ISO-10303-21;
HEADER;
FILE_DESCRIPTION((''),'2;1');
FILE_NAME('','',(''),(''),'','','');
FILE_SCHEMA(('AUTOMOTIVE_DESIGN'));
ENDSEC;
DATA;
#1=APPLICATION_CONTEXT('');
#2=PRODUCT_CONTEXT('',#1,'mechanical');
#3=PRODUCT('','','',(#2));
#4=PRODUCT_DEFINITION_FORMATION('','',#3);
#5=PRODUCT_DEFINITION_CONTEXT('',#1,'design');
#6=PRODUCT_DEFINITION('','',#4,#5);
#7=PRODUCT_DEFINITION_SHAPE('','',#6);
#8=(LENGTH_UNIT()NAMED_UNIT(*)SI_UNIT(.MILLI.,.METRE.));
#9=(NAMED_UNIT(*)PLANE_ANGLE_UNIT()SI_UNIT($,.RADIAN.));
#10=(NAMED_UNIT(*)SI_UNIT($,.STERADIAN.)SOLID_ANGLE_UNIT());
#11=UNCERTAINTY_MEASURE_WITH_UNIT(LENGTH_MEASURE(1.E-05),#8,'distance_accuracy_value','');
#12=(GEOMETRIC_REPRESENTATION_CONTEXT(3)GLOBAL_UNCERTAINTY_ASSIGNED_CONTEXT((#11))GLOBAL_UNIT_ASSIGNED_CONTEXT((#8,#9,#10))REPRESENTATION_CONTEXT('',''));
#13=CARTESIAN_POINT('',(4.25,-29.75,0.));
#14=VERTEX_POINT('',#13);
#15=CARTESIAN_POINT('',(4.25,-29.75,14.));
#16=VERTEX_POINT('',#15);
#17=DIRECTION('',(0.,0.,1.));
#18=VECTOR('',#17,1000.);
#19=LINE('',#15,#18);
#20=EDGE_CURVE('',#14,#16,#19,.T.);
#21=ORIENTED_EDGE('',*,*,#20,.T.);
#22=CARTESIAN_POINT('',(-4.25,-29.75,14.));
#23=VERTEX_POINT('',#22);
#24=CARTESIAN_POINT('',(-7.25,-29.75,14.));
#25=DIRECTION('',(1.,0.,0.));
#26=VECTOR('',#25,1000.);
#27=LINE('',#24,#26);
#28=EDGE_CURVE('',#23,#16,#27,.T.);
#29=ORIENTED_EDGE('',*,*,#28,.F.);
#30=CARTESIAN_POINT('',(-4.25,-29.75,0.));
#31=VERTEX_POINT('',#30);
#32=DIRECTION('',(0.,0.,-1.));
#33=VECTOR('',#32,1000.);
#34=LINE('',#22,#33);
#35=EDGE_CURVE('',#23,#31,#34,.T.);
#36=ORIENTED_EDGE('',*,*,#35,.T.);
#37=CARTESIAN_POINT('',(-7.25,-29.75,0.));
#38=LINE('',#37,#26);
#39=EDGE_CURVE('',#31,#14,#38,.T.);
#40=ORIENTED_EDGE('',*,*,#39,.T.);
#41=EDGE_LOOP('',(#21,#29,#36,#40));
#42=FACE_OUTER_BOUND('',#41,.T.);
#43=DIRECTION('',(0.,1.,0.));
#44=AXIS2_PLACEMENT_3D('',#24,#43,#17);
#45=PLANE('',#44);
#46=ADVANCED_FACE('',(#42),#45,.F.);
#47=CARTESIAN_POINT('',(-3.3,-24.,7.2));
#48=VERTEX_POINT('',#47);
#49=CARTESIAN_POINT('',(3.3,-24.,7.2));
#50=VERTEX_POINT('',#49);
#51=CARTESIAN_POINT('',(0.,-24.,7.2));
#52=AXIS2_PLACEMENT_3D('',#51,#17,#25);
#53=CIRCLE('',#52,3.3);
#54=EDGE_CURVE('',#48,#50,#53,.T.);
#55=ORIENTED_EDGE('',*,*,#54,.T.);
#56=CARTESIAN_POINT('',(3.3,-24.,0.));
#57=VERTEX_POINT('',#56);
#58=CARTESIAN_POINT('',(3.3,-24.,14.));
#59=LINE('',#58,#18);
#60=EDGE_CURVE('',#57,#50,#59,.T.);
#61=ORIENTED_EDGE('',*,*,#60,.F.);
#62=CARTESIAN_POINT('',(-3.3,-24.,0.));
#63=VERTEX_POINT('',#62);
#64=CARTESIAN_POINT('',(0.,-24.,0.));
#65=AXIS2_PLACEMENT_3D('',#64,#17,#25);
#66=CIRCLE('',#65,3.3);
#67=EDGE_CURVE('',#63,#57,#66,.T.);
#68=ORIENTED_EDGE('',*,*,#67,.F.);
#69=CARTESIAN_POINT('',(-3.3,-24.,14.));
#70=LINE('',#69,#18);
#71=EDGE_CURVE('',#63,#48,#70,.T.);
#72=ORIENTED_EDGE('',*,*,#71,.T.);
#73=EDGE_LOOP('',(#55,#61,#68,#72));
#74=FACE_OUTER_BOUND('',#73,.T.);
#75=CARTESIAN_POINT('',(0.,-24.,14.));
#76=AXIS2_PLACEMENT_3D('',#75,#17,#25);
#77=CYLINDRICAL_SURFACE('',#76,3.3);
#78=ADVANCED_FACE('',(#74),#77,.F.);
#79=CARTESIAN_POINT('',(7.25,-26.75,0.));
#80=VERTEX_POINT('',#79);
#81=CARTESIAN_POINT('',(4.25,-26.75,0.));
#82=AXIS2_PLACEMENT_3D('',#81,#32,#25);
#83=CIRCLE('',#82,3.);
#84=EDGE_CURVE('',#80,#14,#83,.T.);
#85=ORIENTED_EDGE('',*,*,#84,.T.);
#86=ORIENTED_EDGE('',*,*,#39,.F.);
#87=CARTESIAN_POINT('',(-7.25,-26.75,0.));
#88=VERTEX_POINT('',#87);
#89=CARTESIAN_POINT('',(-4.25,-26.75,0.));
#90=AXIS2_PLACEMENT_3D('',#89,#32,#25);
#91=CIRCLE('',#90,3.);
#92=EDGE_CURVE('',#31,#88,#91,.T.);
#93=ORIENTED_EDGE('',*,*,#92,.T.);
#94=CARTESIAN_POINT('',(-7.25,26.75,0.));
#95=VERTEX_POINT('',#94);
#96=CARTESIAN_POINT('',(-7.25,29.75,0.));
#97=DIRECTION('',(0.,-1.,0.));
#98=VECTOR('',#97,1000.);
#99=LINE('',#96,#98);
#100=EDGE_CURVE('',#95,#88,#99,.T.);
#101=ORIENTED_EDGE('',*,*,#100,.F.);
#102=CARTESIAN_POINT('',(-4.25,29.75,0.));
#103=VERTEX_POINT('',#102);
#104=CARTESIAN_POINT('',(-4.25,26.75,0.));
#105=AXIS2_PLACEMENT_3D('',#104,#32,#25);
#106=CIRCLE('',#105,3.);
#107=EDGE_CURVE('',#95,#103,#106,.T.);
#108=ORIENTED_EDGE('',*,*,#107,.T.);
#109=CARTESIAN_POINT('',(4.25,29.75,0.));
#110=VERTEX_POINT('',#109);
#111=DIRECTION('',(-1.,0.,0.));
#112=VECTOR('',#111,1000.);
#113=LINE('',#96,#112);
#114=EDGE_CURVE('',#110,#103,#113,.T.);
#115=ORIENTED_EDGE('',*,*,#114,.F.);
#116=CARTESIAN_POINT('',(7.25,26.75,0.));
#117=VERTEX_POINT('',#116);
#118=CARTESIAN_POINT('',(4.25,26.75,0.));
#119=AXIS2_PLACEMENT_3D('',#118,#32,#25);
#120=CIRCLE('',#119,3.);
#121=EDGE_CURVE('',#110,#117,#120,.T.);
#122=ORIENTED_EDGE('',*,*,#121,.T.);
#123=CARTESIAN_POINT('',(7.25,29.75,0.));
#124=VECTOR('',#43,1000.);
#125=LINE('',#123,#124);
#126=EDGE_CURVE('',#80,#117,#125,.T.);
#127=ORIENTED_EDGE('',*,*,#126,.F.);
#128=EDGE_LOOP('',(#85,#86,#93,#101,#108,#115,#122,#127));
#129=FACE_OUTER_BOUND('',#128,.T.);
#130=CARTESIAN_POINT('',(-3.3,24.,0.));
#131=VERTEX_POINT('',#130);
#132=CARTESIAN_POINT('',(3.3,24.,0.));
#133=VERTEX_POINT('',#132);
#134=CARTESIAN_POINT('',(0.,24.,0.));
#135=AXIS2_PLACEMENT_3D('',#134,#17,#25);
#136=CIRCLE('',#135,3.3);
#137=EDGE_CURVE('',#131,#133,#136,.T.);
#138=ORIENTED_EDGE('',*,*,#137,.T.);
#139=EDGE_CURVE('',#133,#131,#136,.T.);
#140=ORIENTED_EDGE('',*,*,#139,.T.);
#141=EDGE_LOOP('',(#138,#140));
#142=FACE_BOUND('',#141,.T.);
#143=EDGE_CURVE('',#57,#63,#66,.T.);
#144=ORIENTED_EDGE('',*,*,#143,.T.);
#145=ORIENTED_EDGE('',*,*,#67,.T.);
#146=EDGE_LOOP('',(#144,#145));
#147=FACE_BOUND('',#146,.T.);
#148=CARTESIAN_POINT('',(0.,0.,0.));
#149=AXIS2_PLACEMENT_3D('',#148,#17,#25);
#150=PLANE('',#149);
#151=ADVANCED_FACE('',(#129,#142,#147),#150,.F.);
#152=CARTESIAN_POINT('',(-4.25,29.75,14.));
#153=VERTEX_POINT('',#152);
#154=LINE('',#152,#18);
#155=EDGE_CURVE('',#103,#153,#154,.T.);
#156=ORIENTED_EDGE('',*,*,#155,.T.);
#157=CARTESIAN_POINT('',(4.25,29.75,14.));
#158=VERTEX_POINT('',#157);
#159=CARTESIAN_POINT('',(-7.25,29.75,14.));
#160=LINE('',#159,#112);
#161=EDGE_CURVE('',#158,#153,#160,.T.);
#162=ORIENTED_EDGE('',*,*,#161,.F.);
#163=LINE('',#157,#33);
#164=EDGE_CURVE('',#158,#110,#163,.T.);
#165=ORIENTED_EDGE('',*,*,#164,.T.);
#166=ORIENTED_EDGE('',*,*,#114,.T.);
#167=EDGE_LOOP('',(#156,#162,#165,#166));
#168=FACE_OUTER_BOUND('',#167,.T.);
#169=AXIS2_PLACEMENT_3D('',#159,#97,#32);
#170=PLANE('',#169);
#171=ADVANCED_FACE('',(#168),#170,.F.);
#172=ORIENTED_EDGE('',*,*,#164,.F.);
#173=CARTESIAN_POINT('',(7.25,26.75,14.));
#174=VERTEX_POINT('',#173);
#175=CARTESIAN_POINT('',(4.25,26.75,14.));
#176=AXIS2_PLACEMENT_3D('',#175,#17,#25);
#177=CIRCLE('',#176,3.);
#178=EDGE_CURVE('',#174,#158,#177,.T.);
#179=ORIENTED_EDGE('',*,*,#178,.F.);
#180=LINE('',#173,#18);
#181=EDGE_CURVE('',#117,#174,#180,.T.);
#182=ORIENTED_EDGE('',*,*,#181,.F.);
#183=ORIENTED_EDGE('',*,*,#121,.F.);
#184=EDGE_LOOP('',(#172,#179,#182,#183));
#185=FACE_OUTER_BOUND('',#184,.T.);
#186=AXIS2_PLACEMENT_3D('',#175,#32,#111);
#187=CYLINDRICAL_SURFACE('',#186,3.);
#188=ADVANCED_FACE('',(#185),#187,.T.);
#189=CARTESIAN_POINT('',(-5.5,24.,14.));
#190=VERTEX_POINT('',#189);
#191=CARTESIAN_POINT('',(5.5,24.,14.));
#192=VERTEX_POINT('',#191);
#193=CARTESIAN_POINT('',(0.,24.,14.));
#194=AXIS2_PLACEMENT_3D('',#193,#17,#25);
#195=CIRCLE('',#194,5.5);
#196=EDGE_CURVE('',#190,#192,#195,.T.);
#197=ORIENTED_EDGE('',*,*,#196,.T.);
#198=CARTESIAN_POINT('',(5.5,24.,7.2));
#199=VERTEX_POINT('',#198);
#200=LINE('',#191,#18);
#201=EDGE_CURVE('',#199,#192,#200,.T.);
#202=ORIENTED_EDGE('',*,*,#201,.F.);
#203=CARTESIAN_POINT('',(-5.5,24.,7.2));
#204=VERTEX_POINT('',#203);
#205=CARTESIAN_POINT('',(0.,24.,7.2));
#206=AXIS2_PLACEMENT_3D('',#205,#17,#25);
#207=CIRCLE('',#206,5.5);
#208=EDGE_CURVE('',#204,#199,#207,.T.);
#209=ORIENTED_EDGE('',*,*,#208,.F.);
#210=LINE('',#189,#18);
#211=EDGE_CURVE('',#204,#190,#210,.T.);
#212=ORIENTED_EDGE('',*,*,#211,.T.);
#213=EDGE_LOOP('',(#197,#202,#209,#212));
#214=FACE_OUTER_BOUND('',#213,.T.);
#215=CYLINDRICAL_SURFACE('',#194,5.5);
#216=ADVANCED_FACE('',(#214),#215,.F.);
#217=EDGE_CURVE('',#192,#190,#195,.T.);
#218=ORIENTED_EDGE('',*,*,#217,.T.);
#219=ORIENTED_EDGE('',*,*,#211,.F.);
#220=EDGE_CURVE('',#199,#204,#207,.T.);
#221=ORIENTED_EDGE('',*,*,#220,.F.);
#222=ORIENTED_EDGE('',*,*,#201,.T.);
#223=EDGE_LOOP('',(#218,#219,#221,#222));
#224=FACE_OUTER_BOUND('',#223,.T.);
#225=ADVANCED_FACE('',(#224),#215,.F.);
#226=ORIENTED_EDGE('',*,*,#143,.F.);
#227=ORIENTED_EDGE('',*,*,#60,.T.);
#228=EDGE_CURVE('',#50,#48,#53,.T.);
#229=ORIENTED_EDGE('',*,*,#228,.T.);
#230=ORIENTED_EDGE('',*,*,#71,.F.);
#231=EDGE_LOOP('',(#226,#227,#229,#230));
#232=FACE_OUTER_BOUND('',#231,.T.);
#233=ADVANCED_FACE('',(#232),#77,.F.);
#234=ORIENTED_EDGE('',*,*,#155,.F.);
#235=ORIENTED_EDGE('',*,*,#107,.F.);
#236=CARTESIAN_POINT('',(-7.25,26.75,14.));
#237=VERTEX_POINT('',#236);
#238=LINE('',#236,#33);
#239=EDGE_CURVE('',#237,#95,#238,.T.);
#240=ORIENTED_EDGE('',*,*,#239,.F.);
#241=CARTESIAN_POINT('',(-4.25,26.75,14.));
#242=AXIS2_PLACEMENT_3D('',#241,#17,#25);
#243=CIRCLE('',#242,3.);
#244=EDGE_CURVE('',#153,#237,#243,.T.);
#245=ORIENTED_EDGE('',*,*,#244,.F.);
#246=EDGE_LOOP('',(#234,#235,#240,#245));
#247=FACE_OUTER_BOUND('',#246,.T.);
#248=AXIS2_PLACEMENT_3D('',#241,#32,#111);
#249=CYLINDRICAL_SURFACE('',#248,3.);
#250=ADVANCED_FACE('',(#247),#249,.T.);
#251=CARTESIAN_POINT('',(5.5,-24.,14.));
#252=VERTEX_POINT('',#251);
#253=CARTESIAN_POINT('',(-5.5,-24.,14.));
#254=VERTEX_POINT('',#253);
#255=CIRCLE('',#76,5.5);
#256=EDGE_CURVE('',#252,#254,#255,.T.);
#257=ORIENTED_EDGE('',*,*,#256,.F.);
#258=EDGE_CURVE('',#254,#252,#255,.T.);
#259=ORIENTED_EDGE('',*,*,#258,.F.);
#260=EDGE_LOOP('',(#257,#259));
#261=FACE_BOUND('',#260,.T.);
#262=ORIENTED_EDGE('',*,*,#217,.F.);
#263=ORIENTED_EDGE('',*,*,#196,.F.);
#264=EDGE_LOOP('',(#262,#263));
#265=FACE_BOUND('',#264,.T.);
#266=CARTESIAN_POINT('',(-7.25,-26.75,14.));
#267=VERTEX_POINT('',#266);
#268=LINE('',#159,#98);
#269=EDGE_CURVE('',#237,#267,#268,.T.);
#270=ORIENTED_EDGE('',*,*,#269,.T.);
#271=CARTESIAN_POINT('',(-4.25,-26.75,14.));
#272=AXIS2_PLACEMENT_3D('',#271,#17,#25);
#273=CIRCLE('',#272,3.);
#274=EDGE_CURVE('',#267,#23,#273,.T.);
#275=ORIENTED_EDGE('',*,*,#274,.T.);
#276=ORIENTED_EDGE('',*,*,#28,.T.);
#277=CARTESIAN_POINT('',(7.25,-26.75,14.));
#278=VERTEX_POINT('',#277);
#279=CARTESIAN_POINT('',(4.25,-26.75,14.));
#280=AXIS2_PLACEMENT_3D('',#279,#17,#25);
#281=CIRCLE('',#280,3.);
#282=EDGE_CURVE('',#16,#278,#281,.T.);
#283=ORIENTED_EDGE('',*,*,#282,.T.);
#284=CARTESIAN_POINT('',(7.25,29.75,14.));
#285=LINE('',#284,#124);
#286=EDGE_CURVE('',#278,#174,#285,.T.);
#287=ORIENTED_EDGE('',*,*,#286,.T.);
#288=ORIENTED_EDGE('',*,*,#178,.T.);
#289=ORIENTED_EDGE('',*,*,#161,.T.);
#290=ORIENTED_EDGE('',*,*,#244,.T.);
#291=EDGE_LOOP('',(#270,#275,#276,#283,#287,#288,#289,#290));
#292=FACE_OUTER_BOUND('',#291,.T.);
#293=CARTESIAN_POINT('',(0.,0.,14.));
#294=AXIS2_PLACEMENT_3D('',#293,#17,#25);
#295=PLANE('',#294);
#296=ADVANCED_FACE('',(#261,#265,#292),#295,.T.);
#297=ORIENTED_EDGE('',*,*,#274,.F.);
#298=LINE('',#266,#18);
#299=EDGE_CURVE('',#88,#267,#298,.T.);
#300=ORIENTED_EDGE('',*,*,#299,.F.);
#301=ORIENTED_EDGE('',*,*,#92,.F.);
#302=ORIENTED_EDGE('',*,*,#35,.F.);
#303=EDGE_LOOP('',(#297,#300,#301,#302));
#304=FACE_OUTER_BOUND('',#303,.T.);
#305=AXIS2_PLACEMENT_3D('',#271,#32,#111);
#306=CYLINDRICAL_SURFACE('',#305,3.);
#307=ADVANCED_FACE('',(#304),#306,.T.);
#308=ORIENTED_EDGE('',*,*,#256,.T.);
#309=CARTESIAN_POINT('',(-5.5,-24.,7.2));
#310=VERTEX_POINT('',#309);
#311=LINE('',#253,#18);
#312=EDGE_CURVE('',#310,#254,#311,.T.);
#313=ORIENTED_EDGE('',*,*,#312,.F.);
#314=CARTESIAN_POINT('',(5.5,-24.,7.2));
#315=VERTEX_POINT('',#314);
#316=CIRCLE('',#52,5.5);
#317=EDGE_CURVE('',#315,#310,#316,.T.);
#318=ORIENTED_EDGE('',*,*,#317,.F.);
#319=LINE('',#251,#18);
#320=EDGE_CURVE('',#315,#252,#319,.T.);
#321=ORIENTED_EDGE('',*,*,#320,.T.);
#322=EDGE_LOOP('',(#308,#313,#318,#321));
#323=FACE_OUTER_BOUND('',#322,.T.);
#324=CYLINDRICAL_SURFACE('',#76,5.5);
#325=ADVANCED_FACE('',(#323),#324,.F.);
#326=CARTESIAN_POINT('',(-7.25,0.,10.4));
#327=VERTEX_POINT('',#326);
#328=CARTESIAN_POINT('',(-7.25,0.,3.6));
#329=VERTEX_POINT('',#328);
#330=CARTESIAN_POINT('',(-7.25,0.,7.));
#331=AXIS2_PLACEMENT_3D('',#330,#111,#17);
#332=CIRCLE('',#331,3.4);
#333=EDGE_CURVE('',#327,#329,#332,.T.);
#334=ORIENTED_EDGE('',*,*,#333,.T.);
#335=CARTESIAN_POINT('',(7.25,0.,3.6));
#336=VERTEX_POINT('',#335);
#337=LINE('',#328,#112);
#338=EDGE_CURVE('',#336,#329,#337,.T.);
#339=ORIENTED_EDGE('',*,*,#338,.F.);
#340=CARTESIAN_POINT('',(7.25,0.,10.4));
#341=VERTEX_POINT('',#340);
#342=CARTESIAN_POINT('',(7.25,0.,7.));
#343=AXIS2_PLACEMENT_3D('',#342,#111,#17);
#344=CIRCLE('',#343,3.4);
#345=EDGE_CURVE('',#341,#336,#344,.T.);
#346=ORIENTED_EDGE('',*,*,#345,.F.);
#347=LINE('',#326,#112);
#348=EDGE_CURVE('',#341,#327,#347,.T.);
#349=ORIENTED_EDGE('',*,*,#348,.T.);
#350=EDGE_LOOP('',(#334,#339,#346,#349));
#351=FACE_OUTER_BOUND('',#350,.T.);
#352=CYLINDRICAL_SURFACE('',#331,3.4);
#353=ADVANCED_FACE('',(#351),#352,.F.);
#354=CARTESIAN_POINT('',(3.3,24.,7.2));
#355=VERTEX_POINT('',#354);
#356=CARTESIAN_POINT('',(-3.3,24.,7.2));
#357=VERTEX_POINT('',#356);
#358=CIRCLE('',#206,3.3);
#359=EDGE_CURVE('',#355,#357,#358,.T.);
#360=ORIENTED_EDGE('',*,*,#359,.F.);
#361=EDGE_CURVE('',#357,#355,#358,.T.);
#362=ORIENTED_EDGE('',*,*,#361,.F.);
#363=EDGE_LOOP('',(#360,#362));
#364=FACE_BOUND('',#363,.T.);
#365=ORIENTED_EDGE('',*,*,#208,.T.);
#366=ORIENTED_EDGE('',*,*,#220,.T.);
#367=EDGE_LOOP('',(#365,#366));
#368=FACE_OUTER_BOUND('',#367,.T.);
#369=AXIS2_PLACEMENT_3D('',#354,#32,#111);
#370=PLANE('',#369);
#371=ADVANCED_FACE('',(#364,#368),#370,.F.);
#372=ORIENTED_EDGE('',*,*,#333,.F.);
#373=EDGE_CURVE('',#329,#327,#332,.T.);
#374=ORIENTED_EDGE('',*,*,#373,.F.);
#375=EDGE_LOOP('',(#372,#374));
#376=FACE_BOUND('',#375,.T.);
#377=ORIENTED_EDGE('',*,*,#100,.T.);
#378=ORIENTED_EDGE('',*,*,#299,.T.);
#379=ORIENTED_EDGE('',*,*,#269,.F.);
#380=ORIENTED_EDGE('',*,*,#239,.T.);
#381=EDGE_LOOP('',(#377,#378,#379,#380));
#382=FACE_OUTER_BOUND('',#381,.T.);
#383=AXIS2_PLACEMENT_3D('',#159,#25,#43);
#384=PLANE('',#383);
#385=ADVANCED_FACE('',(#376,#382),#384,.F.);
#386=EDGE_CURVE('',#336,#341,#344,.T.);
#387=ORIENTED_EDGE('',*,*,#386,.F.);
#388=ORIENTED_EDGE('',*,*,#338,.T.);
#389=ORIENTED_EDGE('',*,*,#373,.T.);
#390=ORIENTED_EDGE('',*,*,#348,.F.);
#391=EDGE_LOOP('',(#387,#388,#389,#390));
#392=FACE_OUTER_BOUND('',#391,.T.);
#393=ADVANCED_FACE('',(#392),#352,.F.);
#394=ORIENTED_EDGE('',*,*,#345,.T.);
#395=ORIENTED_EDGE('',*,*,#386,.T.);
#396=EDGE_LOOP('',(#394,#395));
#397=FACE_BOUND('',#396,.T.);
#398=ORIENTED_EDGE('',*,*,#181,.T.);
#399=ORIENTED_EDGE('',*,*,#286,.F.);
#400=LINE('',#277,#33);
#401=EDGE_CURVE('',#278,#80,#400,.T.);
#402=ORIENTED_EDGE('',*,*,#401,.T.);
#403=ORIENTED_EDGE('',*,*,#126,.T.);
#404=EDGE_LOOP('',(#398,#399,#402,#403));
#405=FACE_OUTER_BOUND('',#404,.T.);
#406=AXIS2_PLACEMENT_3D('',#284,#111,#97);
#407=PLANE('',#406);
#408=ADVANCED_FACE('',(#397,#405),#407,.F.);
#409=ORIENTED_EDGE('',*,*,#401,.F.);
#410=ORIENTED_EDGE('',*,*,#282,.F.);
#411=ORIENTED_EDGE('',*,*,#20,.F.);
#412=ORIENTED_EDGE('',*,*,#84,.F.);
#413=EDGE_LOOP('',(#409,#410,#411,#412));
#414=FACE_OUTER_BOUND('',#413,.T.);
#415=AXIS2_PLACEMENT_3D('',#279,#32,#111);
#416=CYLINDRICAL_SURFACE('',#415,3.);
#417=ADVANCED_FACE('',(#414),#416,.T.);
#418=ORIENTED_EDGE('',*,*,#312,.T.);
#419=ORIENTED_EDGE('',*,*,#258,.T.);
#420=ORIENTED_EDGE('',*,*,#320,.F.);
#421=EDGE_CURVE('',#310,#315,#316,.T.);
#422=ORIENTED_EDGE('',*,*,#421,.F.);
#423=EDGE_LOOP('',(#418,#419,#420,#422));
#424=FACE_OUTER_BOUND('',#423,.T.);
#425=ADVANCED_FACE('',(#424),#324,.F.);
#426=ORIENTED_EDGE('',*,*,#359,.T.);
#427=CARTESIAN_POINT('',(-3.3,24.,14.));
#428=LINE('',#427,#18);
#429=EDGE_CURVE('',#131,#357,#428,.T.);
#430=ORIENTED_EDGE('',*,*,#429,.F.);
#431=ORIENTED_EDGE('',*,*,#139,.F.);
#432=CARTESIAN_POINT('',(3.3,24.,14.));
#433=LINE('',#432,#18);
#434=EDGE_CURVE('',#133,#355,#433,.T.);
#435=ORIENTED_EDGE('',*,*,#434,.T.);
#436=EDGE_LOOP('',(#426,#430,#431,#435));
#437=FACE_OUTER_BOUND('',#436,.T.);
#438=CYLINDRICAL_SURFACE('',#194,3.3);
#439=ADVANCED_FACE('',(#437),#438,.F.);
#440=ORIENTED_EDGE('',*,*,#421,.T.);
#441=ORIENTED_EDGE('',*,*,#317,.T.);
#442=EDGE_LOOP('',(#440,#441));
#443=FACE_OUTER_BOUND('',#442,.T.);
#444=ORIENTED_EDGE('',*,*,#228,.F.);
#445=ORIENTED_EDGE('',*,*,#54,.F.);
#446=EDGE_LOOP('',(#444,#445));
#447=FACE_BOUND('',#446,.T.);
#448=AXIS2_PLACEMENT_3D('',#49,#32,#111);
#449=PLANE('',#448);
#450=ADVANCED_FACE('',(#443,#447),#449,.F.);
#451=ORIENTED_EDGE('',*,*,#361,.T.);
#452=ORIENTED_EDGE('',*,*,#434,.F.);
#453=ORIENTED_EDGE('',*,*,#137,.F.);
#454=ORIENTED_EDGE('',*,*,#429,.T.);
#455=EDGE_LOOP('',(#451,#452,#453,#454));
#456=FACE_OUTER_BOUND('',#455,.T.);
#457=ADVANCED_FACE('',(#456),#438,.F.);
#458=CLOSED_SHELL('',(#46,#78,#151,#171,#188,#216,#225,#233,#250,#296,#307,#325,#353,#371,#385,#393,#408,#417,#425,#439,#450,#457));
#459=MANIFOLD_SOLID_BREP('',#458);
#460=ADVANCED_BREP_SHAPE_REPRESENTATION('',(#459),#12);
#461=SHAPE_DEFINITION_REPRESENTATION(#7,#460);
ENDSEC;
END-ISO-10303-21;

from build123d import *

# Parameters (mm, degrees)
SKETCH_1_W                = 14.5
SKETCH_1_H                = 59.5
EXTRUDE_1_DEPTH           = 14
FILLET_1_R                = 3
HOLE_WIZARD_2_D           = 6.6
HOLE_WIZARD_2_CBORE_D     = 11
HOLE_WIZARD_2_CBORE_DEPTH = 6.8
HOLE_WIZARD_M8_1_D        = 6.8


with BuildPart() as part:
    # 草图1 → 凸台-拉伸1 (new body)
    with BuildSketch(Plane.XY):
        Rectangle(SKETCH_1_W, SKETCH_1_H)
    extrude(amount=EXTRUDE_1_DEPTH)

    # 圆角1
    fillet_1_edges = [part.edges().sort_by_distance(p)[0] for p in [
        (7.25, -29.75, 7),
        (-7.25, -29.75, 7),
        (-7.25, 29.75, 7),
        (7.25, 29.75, 7),
    ]]
    fillet(fillet_1_edges, radius=FILLET_1_R)

    # 打孔尺寸(%根据)内六角圆柱头螺钉的类型2 (through all)
    with Locations(Plane.XY.offset(14)):
        with Locations((0, 24), (0, -24)):
            CounterBoreHole(HOLE_WIZARD_2_D / 2, HOLE_WIZARD_2_CBORE_D / 2, HOLE_WIZARD_2_CBORE_DEPTH)

    # M8 螺纹孔1 (through all)
    with Locations(Plane.ZY.offset(7.25)):
        with Locations((7, 0)):
            Hole(HOLE_WIZARD_M8_1_D / 2)


solid = part.part
